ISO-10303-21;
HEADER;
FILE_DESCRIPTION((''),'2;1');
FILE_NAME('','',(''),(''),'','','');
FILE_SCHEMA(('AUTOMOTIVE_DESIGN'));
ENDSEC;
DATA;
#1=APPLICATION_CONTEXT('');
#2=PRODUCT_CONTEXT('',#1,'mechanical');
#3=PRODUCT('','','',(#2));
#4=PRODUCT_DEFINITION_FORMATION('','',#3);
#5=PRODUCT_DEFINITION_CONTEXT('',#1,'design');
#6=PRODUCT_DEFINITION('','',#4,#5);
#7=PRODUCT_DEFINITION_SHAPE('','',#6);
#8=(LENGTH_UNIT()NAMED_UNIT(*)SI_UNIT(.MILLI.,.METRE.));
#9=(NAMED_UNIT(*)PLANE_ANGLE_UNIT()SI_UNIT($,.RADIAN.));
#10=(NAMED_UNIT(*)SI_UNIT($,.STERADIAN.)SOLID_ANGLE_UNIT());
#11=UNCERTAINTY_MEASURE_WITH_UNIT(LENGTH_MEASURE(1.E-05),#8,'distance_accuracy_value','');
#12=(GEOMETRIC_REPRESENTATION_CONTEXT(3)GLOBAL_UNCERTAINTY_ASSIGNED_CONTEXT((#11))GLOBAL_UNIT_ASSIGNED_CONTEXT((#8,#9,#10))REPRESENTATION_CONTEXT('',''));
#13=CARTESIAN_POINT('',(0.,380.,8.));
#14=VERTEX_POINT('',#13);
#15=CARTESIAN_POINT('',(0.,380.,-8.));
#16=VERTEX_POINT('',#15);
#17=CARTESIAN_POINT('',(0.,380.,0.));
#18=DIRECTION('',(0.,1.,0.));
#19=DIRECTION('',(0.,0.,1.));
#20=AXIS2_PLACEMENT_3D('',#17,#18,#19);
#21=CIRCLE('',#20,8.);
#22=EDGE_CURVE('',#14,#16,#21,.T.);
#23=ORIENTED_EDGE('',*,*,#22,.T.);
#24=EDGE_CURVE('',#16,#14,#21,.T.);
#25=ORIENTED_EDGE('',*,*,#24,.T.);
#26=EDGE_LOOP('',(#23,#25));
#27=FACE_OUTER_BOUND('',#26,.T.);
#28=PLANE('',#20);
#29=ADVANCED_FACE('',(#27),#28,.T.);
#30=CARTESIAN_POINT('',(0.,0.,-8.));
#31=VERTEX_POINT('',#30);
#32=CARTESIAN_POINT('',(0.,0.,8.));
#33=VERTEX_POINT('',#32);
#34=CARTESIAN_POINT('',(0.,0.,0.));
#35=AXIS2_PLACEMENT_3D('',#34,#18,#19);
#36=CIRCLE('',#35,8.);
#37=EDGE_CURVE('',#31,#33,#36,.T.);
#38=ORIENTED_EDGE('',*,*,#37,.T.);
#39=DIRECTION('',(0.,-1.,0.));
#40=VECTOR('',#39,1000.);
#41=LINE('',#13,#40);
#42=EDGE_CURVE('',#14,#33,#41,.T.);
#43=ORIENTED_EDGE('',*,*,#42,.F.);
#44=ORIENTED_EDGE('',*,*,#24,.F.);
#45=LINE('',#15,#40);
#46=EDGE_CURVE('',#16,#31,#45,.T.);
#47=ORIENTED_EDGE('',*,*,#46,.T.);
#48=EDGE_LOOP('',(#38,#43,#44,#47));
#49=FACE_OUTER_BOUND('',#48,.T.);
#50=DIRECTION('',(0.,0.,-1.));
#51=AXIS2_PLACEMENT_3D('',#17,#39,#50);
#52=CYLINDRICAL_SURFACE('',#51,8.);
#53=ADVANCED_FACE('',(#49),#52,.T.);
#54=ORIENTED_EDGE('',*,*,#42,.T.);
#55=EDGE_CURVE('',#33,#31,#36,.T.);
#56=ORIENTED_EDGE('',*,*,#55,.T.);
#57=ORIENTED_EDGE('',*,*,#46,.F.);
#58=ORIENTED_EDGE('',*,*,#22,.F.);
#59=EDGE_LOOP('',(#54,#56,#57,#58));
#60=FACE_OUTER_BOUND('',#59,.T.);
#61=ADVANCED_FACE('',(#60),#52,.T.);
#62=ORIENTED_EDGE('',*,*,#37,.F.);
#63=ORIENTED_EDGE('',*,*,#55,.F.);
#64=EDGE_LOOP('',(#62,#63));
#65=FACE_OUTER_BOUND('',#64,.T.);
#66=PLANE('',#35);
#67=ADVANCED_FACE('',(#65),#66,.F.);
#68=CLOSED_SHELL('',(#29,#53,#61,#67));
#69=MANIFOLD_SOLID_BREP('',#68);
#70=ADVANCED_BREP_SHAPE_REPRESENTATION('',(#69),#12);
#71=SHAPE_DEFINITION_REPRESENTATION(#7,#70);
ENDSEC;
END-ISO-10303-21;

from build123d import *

# Parameters (mm, degrees)
SKETCH1_R           = 8
BOSS_EXTRUDE1_DEPTH = 380


with BuildPart() as part:
    # Sketch1 → Boss-Extrude1 (new body)
    with BuildSketch(Plane(origin=(0, 0, 0), x_dir=(1, 0, 0), z_dir=(0, 1, 0))):
        with Locations(Location((0, 0, 0), (0, 0, 270))):
            Circle(SKETCH1_R)
    extrude(amount=BOSS_EXTRUDE1_DEPTH)


solid = part.part
